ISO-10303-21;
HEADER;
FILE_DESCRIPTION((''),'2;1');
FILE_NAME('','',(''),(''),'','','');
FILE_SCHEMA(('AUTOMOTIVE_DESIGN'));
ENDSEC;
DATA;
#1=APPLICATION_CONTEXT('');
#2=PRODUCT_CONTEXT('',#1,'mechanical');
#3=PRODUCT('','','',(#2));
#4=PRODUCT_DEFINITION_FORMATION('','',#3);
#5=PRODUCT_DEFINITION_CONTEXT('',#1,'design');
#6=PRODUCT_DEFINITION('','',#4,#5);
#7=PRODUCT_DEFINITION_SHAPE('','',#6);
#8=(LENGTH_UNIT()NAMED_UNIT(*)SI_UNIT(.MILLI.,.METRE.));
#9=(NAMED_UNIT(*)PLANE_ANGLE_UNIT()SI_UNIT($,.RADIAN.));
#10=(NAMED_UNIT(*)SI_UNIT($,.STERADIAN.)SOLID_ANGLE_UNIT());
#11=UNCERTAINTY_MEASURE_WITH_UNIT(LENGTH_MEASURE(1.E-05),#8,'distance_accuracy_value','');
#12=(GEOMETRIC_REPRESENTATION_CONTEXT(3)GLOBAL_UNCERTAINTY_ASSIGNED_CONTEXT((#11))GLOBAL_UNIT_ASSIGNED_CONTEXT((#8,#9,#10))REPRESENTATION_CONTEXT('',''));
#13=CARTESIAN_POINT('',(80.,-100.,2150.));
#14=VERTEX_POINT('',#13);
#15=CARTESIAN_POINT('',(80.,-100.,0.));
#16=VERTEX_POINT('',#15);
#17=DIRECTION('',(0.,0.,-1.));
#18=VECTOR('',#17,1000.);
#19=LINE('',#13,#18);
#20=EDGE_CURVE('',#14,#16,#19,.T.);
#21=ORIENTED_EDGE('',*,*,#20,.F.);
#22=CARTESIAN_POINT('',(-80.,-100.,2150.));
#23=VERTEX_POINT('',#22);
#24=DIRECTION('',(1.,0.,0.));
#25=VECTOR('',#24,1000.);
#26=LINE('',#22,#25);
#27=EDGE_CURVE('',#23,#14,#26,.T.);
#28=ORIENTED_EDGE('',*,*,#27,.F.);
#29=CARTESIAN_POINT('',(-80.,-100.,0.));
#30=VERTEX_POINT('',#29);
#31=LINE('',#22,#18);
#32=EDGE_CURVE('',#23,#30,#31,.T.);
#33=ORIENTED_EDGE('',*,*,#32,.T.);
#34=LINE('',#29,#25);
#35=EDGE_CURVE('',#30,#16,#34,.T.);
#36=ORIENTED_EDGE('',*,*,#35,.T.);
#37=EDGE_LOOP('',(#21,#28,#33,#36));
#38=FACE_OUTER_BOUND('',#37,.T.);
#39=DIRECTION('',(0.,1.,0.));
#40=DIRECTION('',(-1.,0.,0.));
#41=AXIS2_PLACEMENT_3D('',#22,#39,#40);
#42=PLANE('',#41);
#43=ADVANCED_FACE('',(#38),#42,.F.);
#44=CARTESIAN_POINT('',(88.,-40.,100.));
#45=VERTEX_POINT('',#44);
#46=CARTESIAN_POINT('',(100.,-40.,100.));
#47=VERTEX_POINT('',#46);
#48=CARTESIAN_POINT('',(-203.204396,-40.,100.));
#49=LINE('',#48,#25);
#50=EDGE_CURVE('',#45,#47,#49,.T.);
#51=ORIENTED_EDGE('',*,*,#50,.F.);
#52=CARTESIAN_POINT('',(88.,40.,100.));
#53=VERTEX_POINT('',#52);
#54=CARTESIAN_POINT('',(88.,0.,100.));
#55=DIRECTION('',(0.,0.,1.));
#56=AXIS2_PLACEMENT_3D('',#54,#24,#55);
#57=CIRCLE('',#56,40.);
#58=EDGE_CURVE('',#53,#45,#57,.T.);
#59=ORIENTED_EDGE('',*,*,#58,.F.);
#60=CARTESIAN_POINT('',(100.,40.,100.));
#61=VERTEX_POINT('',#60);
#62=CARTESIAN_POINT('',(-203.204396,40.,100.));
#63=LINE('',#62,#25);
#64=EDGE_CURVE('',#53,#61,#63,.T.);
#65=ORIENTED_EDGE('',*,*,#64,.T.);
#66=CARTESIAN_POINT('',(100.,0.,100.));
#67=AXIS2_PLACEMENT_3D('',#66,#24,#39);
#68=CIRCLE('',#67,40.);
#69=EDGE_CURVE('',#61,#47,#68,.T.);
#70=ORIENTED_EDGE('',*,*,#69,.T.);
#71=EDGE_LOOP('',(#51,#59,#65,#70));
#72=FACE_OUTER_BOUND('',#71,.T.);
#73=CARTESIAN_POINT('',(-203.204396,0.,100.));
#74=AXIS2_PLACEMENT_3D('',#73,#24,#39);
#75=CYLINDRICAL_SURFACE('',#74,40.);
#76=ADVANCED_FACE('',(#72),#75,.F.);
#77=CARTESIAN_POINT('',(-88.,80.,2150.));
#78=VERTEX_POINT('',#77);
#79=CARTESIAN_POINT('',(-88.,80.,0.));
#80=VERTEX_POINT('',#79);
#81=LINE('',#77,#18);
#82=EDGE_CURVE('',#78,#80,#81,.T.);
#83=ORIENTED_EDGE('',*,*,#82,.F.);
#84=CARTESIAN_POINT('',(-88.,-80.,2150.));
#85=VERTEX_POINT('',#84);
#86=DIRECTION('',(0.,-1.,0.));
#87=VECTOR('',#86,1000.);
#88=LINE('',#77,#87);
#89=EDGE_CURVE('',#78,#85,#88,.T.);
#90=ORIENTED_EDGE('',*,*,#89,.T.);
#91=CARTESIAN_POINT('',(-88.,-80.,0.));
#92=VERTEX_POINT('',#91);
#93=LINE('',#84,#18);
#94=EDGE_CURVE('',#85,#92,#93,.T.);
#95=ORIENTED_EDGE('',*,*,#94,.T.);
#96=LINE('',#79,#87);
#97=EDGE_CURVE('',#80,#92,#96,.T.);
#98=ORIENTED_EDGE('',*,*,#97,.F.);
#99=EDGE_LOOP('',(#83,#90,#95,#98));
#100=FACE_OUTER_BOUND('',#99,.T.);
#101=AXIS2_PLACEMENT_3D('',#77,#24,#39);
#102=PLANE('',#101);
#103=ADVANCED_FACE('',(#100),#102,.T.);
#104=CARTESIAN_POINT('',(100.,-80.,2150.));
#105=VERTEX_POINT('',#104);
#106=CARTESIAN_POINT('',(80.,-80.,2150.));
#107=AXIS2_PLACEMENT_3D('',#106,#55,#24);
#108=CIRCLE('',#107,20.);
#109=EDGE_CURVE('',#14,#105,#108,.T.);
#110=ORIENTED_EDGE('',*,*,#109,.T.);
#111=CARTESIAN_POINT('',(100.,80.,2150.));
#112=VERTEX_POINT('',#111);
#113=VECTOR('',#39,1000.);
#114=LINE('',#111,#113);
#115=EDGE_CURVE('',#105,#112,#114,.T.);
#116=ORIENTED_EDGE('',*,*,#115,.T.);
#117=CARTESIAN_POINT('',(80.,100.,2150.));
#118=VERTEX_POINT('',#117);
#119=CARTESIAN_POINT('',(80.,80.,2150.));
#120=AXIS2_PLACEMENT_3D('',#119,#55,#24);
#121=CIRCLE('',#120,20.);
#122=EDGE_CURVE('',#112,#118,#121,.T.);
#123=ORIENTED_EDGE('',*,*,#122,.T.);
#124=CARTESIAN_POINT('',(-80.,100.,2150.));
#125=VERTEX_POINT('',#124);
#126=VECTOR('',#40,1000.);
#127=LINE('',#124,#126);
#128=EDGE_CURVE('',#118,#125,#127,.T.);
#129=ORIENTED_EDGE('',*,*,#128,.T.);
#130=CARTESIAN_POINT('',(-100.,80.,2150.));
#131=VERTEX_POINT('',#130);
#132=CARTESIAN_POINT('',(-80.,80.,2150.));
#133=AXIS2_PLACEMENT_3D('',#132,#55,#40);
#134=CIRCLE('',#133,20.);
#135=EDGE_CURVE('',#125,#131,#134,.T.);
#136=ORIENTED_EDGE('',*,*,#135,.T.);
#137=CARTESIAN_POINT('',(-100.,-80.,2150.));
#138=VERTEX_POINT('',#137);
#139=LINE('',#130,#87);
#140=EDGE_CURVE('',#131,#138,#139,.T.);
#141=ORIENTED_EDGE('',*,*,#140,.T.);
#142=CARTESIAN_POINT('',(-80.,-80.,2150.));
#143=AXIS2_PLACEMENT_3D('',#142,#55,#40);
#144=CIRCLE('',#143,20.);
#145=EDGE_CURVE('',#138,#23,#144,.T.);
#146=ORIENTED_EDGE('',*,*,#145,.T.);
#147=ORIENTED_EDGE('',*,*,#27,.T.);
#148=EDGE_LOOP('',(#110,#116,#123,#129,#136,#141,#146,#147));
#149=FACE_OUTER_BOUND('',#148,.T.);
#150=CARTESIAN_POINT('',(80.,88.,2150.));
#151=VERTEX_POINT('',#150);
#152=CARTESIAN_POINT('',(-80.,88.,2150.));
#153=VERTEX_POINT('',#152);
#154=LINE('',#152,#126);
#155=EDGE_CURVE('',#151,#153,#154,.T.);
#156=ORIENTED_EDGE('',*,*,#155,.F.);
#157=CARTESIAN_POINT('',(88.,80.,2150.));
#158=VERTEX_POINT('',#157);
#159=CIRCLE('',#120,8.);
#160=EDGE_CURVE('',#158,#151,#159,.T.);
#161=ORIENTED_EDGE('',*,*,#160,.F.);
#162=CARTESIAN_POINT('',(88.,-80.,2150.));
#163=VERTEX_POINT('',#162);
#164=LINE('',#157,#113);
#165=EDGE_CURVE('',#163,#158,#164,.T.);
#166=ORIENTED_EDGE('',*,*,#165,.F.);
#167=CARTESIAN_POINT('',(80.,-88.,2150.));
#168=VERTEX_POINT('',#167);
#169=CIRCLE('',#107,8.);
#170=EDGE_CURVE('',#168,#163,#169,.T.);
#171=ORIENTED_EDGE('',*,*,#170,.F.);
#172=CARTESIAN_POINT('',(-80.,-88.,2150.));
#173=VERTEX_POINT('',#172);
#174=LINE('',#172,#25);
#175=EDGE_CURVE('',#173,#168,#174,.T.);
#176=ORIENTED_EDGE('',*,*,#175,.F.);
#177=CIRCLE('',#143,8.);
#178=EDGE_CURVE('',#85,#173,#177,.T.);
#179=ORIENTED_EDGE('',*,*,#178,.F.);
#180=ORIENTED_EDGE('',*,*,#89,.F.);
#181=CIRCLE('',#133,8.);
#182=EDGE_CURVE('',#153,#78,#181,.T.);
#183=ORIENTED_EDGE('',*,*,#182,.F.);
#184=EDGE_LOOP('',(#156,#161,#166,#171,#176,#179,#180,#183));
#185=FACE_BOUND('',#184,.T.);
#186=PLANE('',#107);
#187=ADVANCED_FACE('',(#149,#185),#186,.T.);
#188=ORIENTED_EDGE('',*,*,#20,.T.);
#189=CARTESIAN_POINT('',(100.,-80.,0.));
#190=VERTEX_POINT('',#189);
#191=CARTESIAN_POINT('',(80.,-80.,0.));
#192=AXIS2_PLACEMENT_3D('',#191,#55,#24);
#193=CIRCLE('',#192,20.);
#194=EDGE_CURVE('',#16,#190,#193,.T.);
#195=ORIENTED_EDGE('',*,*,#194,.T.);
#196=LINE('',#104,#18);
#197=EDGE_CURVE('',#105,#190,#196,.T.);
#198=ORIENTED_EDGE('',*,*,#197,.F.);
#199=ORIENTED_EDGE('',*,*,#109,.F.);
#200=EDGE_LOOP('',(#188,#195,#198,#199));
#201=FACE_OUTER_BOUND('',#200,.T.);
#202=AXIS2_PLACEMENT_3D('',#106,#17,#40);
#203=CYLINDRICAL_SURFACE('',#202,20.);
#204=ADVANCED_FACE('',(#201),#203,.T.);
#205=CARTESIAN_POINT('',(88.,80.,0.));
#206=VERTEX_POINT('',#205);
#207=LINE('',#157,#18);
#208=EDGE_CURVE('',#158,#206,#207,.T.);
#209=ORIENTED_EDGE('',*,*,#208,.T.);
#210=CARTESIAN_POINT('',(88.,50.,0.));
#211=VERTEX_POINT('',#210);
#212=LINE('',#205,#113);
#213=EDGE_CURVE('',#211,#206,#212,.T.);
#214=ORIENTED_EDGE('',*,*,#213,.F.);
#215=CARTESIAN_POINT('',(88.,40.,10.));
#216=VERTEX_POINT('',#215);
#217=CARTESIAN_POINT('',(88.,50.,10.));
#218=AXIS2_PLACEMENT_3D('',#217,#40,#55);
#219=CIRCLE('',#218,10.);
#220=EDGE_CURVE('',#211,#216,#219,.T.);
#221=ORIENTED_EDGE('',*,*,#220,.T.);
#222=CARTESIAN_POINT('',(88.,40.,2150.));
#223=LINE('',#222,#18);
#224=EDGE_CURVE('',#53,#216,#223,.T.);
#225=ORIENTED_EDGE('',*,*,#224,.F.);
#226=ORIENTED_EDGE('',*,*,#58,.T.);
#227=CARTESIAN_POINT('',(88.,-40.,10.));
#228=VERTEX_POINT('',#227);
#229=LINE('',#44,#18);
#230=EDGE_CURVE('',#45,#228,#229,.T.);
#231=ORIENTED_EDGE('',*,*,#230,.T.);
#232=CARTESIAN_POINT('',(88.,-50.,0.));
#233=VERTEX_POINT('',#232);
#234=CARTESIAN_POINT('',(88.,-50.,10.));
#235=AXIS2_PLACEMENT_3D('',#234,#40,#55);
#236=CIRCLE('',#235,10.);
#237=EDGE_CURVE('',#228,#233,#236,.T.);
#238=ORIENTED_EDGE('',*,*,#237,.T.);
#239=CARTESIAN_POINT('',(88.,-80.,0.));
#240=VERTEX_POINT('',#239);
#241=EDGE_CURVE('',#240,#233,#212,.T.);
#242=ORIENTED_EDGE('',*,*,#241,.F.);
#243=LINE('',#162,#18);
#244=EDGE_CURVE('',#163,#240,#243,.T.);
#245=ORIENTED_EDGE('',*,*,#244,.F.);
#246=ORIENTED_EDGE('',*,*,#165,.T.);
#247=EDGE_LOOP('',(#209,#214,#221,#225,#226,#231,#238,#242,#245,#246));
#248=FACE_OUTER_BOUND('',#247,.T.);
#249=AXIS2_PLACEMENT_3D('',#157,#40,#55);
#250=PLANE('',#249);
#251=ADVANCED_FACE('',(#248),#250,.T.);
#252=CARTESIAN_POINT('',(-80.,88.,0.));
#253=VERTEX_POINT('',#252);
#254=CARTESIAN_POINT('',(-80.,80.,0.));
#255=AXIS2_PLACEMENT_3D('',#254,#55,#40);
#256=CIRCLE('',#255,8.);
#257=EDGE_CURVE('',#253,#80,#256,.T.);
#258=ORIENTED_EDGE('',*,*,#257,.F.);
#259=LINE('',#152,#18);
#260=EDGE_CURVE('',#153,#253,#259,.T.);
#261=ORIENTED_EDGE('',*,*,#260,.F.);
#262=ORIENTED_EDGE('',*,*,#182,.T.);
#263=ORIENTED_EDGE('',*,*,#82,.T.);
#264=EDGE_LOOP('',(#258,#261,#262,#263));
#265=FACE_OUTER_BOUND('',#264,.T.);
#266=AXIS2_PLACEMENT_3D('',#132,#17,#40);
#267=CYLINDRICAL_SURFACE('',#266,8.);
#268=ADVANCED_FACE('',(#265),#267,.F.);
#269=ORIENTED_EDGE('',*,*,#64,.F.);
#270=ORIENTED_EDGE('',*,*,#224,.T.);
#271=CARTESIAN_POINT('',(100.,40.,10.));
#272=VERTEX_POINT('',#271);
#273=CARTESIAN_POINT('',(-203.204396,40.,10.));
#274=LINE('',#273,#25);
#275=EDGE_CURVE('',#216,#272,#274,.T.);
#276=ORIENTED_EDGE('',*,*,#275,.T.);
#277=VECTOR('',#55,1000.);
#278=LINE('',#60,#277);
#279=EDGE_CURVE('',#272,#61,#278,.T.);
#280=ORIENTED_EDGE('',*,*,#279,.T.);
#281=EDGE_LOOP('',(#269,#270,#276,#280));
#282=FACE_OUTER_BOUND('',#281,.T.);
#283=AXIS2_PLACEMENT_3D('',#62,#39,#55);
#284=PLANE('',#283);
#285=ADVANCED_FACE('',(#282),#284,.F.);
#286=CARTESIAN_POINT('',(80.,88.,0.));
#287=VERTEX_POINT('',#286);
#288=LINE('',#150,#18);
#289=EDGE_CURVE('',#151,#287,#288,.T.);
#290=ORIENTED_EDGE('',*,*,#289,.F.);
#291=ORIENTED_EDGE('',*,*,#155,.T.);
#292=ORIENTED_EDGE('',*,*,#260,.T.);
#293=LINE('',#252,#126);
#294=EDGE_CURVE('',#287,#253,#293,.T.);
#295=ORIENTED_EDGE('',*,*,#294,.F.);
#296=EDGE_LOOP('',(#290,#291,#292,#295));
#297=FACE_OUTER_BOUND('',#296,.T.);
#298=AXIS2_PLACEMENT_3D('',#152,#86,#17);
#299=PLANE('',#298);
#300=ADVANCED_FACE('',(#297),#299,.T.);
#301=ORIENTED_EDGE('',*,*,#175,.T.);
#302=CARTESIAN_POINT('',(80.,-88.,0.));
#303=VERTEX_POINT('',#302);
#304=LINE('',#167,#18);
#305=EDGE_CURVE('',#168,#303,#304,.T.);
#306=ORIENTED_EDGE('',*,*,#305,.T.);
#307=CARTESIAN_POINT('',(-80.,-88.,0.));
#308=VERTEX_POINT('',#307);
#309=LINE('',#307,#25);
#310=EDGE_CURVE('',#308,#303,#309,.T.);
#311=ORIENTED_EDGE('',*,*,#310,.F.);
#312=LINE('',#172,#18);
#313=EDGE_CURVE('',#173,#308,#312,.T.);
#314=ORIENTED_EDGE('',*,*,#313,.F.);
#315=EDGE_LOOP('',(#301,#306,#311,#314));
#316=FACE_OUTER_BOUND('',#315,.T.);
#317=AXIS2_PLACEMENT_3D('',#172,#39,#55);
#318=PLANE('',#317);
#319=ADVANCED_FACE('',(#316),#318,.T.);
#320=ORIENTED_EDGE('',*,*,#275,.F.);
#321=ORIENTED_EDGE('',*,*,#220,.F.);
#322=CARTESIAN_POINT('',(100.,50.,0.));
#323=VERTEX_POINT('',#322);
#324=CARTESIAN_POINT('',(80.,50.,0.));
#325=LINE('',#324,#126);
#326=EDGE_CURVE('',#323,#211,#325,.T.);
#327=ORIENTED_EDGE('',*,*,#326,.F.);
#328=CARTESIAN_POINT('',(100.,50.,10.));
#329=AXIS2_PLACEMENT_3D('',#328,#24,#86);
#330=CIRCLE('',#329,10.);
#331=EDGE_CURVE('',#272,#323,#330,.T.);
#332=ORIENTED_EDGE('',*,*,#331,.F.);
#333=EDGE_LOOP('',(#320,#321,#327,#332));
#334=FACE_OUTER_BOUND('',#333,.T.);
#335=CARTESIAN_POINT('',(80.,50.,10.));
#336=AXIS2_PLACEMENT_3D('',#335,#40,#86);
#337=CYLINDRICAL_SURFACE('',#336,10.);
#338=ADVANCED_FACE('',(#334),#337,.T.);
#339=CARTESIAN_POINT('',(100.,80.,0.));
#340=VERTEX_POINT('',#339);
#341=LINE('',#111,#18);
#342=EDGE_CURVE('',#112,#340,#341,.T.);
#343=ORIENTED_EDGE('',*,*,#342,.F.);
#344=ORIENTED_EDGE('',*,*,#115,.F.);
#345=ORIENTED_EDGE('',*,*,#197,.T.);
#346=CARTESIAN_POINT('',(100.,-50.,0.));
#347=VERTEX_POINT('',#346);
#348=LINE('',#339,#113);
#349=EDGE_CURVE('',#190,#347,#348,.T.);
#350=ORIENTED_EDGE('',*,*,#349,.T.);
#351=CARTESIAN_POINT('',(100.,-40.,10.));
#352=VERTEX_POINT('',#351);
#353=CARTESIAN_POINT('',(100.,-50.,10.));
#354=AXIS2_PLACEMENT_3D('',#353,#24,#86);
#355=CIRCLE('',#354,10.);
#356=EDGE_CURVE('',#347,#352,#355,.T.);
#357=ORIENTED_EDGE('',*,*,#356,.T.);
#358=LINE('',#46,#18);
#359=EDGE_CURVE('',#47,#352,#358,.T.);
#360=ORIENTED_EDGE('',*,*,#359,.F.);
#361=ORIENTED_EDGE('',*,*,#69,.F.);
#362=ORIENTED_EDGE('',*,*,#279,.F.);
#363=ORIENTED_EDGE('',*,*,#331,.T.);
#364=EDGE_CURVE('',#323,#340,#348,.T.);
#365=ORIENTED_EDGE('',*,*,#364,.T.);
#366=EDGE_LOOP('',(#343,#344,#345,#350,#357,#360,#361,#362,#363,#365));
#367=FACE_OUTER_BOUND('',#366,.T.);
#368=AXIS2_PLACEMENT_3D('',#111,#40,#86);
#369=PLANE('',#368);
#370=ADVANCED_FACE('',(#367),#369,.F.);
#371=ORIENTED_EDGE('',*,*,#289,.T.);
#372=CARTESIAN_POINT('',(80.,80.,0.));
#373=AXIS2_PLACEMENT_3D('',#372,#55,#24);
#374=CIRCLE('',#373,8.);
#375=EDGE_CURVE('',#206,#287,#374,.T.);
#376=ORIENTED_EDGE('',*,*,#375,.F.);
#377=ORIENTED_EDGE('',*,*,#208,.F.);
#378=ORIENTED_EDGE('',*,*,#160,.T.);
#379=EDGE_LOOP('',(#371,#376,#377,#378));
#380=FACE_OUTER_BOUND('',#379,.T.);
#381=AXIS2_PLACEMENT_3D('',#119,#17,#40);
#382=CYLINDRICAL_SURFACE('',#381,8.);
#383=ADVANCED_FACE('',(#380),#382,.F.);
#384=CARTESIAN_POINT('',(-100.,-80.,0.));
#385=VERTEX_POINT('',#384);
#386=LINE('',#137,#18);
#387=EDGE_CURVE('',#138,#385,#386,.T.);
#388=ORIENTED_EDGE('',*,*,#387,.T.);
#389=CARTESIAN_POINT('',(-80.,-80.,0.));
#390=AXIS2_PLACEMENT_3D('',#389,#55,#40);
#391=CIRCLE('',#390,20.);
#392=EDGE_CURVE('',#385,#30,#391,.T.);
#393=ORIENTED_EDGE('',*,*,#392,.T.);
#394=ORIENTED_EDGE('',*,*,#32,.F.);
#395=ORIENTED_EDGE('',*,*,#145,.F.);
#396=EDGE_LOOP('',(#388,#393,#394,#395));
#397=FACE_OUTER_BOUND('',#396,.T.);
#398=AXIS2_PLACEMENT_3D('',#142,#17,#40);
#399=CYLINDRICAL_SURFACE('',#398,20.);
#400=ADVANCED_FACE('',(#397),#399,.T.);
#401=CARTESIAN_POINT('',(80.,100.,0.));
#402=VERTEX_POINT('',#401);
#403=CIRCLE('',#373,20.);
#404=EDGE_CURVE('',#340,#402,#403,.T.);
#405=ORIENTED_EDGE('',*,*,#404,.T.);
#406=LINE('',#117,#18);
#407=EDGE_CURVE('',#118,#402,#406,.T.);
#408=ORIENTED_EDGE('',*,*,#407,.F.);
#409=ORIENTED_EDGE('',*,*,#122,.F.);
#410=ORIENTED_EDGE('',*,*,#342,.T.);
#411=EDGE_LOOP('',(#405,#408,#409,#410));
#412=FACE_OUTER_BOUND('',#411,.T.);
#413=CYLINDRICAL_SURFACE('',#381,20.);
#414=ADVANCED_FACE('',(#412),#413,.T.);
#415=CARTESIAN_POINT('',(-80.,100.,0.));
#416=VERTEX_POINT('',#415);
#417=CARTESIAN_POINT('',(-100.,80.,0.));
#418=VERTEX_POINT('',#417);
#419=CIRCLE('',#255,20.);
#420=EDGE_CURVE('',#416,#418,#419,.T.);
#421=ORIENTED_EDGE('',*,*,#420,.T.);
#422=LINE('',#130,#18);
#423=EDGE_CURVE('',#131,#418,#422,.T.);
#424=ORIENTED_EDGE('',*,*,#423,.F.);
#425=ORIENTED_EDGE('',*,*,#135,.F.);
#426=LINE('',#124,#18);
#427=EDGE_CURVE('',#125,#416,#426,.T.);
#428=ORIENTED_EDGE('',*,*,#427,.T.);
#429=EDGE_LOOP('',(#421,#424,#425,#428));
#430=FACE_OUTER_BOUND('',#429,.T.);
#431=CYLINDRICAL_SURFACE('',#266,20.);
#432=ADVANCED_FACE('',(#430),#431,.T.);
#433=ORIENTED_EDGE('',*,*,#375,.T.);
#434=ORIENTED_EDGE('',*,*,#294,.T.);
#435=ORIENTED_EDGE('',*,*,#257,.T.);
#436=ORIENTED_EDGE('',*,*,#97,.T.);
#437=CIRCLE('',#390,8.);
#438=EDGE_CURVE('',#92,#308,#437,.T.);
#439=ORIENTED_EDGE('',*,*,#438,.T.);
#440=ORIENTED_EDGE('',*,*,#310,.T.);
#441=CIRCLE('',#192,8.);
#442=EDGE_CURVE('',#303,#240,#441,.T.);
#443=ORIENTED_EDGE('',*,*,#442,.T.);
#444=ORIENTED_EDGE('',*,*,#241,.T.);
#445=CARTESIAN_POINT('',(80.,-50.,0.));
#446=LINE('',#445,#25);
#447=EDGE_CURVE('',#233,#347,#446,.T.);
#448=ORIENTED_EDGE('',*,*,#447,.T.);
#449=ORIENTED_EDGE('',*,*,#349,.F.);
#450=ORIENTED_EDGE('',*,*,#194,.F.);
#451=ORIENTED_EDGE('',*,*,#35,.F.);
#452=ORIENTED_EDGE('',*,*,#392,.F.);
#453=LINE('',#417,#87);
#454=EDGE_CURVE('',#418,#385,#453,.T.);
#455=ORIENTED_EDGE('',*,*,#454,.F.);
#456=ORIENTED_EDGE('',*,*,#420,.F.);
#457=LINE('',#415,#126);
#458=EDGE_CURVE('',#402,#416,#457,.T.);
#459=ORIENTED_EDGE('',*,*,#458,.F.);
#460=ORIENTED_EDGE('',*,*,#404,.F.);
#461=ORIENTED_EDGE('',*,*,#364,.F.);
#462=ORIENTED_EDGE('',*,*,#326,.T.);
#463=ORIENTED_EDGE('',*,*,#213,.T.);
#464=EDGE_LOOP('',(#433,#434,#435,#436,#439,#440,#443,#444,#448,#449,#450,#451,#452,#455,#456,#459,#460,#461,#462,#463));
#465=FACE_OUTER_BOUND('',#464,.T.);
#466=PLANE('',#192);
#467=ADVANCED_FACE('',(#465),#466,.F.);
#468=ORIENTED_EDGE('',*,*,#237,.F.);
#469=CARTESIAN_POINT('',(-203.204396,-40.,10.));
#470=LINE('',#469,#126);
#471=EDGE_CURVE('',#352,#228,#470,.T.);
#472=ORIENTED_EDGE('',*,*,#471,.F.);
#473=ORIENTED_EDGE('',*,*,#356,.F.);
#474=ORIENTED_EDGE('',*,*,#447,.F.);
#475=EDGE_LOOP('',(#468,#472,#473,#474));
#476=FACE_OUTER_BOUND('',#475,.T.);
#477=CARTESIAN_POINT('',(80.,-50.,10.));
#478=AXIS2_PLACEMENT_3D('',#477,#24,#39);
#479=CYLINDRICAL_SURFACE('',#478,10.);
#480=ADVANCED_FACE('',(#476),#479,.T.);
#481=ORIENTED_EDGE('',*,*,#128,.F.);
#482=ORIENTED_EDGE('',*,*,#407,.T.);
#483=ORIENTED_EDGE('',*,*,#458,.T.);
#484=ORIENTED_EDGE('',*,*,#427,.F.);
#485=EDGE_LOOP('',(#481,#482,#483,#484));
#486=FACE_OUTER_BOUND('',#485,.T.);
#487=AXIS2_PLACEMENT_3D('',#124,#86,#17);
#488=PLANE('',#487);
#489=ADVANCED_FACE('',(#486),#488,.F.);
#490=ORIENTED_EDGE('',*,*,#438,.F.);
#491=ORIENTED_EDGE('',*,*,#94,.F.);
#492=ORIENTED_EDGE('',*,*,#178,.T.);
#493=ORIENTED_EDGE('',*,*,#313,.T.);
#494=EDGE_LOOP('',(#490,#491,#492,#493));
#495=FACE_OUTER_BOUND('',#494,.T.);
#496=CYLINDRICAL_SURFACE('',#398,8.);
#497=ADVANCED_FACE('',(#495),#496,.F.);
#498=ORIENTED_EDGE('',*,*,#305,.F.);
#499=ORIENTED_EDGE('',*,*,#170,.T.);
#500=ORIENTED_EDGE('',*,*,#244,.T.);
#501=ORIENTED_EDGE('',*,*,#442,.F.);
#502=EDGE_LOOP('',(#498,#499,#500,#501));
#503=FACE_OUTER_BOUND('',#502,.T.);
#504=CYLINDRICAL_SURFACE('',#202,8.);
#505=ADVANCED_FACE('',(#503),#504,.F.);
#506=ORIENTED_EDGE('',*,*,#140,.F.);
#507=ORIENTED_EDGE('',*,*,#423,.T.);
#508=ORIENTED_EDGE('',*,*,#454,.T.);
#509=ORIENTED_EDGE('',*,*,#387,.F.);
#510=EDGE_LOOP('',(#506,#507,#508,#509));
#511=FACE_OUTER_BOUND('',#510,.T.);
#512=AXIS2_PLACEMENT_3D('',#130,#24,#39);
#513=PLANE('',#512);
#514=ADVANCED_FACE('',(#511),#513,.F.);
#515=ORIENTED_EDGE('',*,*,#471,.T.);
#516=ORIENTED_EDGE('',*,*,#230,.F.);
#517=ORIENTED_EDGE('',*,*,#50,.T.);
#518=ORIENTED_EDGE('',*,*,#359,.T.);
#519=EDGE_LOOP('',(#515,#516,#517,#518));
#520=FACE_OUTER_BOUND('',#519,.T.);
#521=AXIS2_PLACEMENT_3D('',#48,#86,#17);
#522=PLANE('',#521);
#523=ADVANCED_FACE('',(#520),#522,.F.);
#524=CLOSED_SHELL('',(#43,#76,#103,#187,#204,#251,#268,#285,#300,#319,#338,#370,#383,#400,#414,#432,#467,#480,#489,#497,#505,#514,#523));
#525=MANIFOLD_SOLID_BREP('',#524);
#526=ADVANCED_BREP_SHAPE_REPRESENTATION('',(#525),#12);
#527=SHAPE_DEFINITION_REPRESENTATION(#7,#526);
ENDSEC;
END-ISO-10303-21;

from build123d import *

# Parameters (mm, degrees)
EXTRUDE_1_DEPTH     = 2150
CUT_EXTRUDE_2_DEPTH = 12
FILLET_1_R          = 10


with BuildPart() as part:
    # 草图1 → 凸台-拉伸1 (new body)
    with BuildSketch(Plane.XY):
        with BuildLine():
            Line((-80, 100), (80, 100))
            ThreePointArc((80, 100), (94.142135624, 94.142135624), (100, 80))
            Line((100, 80), (100, -80))
            ThreePointArc((100, -80), (94.142135624, -94.142135624), (80, -100))
            Line((80, -100), (-80, -100))
            ThreePointArc((-80, -100), (-94.142135624, -94.142135624), (-100, -80))
            Line((-100, -80), (-100, 80))
            ThreePointArc((-100, 80), (-94.142135624, 94.142135624), (-80, 100))
        make_face()
        with BuildLine():
            Line((-80, 88), (80, 88))
            ThreePointArc((80, 88), (85.656854249, 85.656854249), (88, 80))
            Line((88, 80), (88, -80))
            ThreePointArc((88, -80), (85.656854249, -85.656854249), (80, -88))
            Line((80, -88), (-80, -88))
            ThreePointArc((-80, -88), (-85.656854249, -85.656854249), (-88, -80))
            Line((-88, -80), (-88, 80))
            ThreePointArc((-88, 80), (-85.656854249, 85.656854249), (-80, 88))
        make_face(mode=Mode.SUBTRACT)
    extrude(amount=EXTRUDE_1_DEPTH)

    # 草图3 → 切除-拉伸2 (cut)
    with BuildSketch(Plane(origin=(100, 0, 0), x_dir=(0, 0, -1), z_dir=(1, 0, 0))):
        with BuildLine():
            Line((-100, 40), (100, 40))
            ThreePointArc((100, 40), (140, 0), (100, -40))
            Line((100, -40), (-100, -40))
            ThreePointArc((-100, -40), (-140, 0), (-100, 40))
        make_face()
    extrude(amount=-CUT_EXTRUDE_2_DEPTH, mode=Mode.SUBTRACT)

    # 圆角1
    fillet_1_edges = [part.edges().sort_by_distance(p)[0] for p in [
        (94, -40, 0),
        (94, 40, 0),
    ]]
    fillet(fillet_1_edges, radius=FILLET_1_R)


solid = part.part
